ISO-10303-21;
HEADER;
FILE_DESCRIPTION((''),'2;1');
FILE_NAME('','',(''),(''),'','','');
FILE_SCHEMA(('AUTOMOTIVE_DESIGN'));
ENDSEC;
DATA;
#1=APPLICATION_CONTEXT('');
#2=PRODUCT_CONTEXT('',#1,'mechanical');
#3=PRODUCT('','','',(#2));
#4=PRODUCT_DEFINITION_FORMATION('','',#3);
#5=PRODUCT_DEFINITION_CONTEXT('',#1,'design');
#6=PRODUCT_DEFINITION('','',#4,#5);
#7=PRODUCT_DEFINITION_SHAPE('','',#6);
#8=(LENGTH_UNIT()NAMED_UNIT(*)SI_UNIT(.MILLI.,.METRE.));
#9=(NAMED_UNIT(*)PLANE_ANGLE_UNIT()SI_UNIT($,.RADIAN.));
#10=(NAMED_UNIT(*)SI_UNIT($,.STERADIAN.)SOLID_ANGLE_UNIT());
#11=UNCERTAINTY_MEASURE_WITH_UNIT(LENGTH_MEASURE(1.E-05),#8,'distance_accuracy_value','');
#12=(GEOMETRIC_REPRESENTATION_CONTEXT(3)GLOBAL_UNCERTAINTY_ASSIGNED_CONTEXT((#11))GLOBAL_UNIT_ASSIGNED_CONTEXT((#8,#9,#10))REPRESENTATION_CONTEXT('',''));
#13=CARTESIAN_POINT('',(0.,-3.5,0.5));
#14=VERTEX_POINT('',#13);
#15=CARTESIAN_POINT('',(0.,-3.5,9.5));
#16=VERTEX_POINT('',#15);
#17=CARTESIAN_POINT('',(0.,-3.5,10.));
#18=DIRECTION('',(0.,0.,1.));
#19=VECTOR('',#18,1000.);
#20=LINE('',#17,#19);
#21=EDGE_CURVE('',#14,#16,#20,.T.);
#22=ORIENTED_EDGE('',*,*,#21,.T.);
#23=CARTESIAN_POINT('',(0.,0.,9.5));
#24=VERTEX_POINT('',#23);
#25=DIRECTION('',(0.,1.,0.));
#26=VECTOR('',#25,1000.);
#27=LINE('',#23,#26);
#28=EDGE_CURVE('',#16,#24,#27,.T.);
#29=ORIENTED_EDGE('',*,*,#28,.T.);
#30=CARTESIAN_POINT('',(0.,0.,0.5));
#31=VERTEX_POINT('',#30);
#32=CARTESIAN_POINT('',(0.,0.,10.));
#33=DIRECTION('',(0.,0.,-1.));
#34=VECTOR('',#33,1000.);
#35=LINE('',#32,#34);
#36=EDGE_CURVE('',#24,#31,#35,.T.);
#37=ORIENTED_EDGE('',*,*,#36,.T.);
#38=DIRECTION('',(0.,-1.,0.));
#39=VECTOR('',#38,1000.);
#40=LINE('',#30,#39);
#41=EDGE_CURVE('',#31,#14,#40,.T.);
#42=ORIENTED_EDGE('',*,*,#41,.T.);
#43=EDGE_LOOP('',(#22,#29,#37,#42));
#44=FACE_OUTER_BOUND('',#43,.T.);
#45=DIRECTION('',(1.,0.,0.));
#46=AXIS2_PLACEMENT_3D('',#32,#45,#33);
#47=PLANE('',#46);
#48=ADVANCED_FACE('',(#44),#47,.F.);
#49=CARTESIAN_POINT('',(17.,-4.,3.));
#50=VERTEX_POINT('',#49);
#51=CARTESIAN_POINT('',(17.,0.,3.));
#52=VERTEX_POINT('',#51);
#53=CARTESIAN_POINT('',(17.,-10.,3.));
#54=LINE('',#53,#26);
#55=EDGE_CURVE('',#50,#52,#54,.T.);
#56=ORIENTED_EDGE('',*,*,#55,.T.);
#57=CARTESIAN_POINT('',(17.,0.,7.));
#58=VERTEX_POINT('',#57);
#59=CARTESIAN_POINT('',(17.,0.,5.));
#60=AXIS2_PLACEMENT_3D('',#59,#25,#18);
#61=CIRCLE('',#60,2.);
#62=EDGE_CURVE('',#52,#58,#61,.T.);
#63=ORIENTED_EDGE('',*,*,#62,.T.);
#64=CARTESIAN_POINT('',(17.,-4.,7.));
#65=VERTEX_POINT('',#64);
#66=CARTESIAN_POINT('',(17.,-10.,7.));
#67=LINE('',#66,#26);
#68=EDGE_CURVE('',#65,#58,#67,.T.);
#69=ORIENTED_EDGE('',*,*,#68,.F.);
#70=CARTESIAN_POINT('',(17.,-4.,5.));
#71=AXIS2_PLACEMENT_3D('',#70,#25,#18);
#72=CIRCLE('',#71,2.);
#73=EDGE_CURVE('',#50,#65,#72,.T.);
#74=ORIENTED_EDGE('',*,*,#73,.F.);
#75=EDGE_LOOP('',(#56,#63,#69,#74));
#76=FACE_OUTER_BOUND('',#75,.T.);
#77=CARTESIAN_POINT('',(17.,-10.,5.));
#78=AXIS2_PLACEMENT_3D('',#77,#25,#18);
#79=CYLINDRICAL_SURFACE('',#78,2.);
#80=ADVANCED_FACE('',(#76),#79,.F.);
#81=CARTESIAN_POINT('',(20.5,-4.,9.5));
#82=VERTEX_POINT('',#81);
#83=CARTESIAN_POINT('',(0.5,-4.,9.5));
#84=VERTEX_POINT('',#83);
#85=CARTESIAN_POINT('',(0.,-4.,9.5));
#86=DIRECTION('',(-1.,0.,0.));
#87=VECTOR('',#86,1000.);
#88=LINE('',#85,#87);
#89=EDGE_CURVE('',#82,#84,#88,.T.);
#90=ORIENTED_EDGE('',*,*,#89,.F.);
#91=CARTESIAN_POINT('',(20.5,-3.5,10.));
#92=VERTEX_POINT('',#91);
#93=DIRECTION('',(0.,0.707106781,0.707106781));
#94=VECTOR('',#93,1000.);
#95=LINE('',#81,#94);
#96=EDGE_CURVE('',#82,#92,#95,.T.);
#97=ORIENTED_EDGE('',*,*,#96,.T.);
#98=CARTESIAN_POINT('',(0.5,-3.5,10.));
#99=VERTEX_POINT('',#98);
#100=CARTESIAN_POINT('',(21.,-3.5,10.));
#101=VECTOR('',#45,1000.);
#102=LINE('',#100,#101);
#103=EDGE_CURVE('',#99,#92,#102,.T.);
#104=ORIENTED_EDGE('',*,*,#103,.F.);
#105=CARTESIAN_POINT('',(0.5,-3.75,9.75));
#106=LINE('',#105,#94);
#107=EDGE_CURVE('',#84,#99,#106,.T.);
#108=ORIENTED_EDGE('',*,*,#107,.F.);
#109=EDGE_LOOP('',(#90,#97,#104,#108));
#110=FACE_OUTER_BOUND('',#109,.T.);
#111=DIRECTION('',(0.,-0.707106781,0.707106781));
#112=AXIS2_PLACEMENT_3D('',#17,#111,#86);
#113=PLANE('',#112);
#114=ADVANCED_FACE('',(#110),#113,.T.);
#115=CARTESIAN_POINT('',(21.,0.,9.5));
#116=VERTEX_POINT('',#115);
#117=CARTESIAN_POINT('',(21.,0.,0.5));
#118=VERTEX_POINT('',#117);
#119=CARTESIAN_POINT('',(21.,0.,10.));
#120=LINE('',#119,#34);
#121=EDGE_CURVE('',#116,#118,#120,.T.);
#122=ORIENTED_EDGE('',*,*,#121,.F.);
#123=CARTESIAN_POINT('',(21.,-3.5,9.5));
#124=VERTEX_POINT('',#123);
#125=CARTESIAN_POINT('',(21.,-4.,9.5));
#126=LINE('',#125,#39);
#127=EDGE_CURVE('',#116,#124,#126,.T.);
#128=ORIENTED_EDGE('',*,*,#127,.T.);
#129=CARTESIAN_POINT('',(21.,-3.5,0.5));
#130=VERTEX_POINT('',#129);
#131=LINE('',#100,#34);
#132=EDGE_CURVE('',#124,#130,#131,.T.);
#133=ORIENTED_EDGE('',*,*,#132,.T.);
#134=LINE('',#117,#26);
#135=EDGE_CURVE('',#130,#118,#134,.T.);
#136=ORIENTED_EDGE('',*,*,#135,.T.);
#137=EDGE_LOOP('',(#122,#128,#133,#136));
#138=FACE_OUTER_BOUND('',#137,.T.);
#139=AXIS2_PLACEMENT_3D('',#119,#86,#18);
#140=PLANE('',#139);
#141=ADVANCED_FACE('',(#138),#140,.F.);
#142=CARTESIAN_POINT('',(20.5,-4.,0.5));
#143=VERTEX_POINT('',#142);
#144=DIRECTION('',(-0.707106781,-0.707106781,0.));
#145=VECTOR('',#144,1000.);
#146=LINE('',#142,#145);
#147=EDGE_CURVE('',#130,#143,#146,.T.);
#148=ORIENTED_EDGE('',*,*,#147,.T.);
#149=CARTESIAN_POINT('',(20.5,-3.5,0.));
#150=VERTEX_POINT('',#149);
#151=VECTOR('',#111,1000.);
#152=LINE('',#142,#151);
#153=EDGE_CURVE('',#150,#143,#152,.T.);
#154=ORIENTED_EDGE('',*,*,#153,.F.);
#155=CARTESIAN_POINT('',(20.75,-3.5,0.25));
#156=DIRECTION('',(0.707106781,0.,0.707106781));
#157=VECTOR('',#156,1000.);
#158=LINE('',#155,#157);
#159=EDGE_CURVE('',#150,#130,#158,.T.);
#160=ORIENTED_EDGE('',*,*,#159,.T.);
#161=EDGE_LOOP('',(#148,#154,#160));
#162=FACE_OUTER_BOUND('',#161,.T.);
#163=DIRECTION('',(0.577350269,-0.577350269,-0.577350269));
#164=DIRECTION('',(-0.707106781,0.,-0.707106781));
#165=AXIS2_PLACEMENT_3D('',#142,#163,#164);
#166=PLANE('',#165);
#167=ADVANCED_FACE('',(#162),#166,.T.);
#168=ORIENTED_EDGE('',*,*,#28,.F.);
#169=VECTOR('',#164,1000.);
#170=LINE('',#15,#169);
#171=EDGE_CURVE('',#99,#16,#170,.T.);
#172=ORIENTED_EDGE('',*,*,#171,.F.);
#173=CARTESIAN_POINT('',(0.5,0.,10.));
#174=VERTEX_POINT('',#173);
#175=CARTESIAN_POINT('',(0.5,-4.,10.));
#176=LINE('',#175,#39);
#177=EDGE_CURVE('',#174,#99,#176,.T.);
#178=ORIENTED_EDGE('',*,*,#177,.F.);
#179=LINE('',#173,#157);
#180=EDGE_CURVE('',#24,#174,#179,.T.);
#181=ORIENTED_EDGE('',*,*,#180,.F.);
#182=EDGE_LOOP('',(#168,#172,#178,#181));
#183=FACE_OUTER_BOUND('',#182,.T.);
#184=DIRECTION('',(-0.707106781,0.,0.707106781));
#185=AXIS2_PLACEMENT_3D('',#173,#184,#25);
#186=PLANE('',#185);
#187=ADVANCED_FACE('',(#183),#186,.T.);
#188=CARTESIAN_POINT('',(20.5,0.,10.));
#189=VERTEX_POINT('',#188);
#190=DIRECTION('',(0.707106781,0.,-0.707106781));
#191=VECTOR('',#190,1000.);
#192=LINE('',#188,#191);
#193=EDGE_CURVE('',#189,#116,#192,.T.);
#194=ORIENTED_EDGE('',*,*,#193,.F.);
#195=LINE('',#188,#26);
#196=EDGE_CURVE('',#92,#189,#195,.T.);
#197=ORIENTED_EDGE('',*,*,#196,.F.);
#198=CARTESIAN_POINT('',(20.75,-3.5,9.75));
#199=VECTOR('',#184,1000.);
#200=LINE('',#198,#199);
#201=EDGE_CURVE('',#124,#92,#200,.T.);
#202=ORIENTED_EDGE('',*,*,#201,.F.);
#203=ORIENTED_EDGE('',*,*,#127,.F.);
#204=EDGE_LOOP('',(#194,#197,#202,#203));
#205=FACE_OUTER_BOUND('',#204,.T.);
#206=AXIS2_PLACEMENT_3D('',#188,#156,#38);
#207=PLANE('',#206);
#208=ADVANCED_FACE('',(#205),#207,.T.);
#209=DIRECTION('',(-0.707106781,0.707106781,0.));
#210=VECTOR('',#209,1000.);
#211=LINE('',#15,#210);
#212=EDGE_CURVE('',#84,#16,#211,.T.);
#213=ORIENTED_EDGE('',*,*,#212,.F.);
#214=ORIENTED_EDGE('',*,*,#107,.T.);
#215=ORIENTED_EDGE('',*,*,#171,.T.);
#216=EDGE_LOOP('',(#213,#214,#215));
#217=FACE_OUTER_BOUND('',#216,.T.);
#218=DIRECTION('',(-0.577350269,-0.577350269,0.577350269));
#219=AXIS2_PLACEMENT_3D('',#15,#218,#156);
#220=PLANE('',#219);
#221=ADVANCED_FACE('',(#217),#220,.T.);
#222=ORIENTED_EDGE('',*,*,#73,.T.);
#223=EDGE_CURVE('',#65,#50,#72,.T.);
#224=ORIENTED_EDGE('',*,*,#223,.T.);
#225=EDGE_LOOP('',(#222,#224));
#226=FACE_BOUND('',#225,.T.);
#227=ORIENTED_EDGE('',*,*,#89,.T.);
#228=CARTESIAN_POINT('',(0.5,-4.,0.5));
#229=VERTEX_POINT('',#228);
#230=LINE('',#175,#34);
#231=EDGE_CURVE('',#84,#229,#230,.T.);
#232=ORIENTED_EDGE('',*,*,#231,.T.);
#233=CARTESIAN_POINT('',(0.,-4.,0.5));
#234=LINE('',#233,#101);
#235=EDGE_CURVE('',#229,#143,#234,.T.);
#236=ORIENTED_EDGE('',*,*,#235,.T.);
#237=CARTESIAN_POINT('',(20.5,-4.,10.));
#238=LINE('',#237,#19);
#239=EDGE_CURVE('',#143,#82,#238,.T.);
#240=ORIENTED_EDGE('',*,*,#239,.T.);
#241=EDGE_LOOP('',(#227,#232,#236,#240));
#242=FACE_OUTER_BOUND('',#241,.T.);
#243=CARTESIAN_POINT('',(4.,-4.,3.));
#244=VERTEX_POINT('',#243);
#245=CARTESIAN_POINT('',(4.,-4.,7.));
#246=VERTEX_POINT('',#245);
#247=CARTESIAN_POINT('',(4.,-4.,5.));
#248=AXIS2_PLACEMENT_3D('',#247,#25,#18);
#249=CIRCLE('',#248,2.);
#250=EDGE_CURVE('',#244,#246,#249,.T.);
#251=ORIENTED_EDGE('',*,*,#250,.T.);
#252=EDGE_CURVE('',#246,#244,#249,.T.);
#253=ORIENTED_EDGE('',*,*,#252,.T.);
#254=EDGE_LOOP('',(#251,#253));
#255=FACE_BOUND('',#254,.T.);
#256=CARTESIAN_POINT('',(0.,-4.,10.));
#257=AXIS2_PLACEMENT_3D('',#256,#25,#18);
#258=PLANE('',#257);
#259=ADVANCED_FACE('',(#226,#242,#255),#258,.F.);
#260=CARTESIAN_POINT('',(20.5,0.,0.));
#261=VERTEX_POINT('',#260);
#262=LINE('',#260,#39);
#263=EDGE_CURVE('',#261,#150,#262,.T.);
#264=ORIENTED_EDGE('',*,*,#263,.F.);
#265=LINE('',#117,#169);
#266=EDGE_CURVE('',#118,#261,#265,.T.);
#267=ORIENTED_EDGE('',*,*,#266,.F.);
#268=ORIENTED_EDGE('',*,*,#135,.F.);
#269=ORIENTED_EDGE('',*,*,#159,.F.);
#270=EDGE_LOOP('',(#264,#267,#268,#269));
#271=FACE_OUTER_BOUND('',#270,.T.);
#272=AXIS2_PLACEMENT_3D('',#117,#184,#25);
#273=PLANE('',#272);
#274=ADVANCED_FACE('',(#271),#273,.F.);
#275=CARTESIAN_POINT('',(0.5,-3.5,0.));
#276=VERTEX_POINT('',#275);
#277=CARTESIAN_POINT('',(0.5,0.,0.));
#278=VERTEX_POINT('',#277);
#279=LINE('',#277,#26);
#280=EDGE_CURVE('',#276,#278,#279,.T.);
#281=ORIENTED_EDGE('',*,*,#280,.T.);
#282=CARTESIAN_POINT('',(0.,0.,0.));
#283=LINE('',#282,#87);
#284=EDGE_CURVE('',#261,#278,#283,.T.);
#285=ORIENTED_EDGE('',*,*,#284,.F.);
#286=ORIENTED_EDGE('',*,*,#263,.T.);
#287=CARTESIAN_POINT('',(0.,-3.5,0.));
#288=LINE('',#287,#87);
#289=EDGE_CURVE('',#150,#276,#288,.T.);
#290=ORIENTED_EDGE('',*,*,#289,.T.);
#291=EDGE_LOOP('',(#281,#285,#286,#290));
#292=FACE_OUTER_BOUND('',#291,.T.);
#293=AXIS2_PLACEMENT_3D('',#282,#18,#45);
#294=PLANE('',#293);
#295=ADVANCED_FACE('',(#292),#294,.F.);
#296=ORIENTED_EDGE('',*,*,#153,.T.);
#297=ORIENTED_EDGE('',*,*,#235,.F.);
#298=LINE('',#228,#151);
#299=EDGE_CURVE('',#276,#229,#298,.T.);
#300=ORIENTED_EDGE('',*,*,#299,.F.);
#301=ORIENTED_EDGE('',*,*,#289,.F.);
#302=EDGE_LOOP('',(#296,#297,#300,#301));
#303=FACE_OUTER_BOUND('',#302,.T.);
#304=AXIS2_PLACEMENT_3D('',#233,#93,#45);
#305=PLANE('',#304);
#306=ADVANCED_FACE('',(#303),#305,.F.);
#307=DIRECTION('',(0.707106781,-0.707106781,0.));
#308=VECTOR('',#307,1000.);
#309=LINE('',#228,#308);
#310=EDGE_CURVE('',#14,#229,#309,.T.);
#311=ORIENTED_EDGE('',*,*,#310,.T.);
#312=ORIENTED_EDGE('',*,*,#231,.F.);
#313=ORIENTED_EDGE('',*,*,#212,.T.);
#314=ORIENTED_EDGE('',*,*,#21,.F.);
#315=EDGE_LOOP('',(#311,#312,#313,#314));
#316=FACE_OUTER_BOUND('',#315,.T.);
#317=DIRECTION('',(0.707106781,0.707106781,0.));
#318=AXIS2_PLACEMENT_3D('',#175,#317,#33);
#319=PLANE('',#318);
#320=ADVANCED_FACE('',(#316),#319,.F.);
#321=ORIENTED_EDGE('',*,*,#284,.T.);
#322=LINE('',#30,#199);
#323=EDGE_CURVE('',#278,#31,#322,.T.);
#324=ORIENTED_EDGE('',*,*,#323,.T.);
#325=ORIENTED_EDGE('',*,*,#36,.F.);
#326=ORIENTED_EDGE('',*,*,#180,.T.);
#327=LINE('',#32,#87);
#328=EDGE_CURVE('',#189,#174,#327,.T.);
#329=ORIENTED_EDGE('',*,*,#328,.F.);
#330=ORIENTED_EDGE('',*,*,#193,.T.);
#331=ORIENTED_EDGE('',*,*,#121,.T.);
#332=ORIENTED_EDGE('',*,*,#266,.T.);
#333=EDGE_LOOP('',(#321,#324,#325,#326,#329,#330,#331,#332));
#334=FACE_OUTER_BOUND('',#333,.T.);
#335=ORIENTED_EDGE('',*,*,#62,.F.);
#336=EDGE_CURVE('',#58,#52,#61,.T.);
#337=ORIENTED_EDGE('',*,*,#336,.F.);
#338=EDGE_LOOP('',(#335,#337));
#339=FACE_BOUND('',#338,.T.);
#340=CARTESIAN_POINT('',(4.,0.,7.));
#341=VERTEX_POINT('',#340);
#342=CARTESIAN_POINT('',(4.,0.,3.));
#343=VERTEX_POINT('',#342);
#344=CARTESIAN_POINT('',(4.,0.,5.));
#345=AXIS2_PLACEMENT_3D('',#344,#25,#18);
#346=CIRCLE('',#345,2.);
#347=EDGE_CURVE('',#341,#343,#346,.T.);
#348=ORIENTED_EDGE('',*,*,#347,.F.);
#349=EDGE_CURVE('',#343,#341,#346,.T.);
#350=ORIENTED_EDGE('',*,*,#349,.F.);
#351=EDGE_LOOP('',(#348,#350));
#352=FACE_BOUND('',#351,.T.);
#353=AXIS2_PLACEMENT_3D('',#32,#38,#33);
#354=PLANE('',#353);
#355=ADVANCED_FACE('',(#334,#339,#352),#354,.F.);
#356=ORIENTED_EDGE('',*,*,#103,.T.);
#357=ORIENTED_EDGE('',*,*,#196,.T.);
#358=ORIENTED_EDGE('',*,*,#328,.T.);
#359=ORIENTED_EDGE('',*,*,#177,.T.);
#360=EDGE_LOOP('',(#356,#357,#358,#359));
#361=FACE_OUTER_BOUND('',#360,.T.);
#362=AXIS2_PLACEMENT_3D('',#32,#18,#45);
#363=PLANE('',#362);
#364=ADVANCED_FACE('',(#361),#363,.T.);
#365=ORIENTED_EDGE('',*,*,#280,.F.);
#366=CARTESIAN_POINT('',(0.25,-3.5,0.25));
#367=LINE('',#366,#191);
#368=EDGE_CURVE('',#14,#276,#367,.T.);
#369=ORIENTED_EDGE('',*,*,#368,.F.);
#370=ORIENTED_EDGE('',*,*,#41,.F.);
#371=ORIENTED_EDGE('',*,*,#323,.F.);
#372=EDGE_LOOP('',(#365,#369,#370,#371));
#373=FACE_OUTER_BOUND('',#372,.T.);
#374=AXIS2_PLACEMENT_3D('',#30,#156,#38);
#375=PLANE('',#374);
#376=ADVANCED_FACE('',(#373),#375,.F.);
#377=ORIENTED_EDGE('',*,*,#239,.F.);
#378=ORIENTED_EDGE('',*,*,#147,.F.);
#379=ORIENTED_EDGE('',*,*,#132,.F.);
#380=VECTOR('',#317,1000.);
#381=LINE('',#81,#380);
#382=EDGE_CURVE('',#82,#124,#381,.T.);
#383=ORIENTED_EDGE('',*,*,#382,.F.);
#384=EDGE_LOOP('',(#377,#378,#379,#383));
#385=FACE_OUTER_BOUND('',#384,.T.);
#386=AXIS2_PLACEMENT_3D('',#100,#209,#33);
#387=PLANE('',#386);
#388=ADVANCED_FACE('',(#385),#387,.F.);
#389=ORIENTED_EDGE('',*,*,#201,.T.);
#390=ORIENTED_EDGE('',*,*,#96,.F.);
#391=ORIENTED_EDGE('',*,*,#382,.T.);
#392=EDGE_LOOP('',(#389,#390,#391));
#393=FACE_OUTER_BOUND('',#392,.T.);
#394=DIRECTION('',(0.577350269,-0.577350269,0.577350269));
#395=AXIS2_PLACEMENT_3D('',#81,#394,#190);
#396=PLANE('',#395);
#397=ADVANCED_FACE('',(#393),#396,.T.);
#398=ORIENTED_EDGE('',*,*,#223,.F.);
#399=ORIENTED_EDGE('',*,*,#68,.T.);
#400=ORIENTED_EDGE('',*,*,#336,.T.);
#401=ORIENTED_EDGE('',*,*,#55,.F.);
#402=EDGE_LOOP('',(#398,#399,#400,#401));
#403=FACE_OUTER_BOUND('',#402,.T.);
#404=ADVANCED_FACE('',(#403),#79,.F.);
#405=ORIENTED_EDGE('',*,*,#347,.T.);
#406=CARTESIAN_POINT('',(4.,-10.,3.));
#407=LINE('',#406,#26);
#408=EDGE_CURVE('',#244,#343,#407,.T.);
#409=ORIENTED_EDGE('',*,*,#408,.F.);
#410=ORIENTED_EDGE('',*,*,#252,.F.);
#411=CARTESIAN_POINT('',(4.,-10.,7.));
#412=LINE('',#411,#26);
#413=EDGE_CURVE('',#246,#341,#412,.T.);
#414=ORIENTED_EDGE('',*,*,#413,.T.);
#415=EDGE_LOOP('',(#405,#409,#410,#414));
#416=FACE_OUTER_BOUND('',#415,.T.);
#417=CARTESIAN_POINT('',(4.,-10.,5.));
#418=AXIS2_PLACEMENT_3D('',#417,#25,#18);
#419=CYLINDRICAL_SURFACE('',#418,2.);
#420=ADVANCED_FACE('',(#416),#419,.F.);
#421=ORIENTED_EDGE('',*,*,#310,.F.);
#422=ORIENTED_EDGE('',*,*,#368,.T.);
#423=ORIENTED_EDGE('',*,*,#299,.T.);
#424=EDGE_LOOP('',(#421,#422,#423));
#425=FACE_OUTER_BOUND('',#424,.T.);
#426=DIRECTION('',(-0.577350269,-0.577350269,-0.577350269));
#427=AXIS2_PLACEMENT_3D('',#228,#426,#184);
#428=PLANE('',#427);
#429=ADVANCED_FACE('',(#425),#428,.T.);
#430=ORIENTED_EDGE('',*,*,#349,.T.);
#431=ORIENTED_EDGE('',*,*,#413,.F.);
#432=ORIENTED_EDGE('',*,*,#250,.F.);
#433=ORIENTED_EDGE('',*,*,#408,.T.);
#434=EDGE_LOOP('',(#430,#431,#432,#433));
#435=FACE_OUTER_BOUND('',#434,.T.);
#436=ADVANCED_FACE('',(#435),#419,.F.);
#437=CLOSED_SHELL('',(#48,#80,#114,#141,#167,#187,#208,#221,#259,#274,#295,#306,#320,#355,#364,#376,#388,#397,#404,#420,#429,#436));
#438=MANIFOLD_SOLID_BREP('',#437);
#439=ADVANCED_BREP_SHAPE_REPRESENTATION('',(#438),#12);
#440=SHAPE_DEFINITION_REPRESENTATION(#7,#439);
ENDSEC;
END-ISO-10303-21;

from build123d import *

# Parameters (mm, degrees)
SKETCH1_W           = 21
SKETCH1_H           = 4
BOSS_EXTRUDE1_DEPTH = 10
SKETCH2_R           = 2
CUT_EXTRUDE1_DEPTH  = 10
CHAMFER2_SIZE       = 0.5


with BuildPart() as part:
    # Sketch1 → Boss-Extrude1 (new body)
    with BuildSketch(Plane.XY):
        with Locations((10.5, -2)):
            Rectangle(SKETCH1_W, SKETCH1_H)
    extrude(amount=BOSS_EXTRUDE1_DEPTH)

    # Sketch2 → Cut-Extrude1 (cut)
    with BuildSketch(Plane(origin=(0, 0, 0), x_dir=(1, 0, 0), z_dir=(0, 1, 0))):
        with Locations(Location((17, -5, 0), (0, 0, 270))):
            Circle(SKETCH2_R)
        with Locations(Location((4, -5, 0), (0, 0, 270))):
            Circle(SKETCH2_R)
    extrude(amount=-CUT_EXTRUDE1_DEPTH, mode=Mode.SUBTRACT)

    # Chamfer2
    chamfer2_edges = [part.edges().sort_by_distance(p)[0] for p in [
        (21, -2, 10),
        (0, -2, 10),
        (21, -2, 0),
        (10.5, -4, 0),
        (0, -2, 0),
        (10.5, -4, 10),
        (21, -4, 5),
        (0, -4, 5),
    ]]
    chamfer(chamfer2_edges, length=CHAMFER2_SIZE)


solid = part.part
